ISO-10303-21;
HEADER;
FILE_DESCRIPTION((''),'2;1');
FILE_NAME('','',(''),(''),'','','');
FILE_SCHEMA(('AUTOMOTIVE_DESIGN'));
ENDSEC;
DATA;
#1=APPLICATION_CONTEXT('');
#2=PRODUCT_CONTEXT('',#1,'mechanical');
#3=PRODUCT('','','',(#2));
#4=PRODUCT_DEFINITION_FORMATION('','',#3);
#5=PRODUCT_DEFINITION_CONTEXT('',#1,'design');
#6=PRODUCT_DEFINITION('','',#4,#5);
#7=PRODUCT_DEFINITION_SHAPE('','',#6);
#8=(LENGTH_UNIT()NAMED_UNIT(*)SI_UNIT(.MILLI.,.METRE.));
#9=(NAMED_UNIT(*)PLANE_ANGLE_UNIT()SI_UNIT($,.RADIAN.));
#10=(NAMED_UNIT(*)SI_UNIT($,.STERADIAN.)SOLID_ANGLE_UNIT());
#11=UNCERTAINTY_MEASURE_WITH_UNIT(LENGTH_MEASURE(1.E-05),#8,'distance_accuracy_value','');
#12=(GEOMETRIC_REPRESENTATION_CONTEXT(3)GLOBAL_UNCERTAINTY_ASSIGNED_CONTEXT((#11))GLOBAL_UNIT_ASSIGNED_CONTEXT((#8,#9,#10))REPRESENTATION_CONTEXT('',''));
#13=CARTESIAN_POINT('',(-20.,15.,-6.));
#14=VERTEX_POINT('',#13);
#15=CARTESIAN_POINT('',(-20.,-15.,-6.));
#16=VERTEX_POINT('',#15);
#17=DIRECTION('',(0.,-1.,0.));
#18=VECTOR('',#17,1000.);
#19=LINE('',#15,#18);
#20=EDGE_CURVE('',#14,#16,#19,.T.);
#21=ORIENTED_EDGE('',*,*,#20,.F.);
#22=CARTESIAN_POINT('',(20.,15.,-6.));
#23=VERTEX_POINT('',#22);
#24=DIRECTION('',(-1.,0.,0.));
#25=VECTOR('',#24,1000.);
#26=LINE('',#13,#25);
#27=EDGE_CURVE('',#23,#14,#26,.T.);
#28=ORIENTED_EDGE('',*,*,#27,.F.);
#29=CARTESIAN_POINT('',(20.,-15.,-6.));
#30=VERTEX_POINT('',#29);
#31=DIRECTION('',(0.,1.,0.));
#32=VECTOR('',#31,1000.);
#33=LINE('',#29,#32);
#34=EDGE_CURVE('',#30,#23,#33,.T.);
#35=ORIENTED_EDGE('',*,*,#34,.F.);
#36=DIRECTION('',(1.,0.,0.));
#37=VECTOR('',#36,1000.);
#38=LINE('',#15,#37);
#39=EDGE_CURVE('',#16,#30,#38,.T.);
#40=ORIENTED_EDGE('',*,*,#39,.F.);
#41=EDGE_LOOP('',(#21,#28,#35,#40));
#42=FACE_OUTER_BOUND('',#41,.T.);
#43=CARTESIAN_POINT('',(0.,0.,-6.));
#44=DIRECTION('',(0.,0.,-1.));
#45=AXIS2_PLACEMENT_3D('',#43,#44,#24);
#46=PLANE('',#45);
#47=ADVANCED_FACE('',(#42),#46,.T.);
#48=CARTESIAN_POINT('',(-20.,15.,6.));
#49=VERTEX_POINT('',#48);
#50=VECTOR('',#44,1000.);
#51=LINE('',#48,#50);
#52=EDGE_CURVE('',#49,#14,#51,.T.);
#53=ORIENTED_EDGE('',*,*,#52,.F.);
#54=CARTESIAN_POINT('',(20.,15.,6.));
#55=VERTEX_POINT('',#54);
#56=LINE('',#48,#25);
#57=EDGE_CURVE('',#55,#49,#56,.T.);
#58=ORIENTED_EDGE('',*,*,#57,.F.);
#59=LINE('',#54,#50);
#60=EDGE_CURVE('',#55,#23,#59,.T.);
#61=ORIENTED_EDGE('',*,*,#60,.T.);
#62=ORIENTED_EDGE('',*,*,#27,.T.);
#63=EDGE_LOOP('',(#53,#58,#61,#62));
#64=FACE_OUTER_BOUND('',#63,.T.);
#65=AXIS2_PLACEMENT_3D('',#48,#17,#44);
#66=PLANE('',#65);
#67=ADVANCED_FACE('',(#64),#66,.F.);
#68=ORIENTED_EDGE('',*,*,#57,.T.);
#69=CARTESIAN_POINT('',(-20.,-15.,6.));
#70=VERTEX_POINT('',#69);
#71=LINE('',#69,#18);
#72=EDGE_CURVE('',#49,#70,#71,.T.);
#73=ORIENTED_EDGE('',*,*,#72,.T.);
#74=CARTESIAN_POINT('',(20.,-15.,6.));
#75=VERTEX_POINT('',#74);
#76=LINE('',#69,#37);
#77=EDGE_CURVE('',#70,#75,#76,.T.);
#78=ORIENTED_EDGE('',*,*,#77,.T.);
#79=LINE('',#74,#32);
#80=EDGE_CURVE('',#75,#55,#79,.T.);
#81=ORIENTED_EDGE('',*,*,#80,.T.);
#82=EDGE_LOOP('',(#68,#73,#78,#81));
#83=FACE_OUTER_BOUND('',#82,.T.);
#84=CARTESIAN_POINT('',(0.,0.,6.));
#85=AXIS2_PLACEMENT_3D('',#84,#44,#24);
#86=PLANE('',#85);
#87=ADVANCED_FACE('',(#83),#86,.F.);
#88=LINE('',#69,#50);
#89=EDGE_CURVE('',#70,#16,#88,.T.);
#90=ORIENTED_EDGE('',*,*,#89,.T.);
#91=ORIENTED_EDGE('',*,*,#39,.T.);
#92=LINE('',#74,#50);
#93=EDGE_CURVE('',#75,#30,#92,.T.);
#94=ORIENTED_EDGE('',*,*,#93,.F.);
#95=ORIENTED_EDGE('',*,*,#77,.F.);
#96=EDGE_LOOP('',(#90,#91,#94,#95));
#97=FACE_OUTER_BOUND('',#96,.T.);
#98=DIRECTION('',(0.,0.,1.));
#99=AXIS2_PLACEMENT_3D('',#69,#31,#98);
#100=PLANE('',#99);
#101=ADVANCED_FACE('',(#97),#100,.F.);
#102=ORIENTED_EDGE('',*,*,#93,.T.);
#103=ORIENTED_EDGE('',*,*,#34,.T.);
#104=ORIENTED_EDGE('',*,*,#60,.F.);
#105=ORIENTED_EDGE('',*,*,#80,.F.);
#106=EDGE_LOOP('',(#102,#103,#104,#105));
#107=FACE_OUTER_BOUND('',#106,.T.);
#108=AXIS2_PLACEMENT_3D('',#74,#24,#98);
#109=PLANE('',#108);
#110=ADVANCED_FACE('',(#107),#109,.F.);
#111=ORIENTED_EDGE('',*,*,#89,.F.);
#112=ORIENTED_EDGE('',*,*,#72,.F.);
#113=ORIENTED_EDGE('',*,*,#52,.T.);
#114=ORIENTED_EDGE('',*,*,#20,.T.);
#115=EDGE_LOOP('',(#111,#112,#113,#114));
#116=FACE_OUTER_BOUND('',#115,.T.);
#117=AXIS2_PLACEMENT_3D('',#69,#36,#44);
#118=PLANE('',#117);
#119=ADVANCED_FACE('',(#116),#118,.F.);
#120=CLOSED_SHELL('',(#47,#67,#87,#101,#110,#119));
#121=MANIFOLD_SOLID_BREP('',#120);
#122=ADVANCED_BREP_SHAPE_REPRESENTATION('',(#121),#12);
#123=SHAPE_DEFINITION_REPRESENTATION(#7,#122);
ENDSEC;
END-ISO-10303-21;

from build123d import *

# Parameters (mm, degrees)
SKETCH_1_W      = 40
SKETCH_1_H      = 30
EXTRUDE_1_DEPTH = 6


with BuildPart() as part:
    # 草图1 → 凸台-拉伸1 (new, symmetric)
    with BuildSketch(Plane.XY):
        Rectangle(SKETCH_1_W, SKETCH_1_H)
    extrude(amount=EXTRUDE_1_DEPTH, both=True)


solid = part.part
